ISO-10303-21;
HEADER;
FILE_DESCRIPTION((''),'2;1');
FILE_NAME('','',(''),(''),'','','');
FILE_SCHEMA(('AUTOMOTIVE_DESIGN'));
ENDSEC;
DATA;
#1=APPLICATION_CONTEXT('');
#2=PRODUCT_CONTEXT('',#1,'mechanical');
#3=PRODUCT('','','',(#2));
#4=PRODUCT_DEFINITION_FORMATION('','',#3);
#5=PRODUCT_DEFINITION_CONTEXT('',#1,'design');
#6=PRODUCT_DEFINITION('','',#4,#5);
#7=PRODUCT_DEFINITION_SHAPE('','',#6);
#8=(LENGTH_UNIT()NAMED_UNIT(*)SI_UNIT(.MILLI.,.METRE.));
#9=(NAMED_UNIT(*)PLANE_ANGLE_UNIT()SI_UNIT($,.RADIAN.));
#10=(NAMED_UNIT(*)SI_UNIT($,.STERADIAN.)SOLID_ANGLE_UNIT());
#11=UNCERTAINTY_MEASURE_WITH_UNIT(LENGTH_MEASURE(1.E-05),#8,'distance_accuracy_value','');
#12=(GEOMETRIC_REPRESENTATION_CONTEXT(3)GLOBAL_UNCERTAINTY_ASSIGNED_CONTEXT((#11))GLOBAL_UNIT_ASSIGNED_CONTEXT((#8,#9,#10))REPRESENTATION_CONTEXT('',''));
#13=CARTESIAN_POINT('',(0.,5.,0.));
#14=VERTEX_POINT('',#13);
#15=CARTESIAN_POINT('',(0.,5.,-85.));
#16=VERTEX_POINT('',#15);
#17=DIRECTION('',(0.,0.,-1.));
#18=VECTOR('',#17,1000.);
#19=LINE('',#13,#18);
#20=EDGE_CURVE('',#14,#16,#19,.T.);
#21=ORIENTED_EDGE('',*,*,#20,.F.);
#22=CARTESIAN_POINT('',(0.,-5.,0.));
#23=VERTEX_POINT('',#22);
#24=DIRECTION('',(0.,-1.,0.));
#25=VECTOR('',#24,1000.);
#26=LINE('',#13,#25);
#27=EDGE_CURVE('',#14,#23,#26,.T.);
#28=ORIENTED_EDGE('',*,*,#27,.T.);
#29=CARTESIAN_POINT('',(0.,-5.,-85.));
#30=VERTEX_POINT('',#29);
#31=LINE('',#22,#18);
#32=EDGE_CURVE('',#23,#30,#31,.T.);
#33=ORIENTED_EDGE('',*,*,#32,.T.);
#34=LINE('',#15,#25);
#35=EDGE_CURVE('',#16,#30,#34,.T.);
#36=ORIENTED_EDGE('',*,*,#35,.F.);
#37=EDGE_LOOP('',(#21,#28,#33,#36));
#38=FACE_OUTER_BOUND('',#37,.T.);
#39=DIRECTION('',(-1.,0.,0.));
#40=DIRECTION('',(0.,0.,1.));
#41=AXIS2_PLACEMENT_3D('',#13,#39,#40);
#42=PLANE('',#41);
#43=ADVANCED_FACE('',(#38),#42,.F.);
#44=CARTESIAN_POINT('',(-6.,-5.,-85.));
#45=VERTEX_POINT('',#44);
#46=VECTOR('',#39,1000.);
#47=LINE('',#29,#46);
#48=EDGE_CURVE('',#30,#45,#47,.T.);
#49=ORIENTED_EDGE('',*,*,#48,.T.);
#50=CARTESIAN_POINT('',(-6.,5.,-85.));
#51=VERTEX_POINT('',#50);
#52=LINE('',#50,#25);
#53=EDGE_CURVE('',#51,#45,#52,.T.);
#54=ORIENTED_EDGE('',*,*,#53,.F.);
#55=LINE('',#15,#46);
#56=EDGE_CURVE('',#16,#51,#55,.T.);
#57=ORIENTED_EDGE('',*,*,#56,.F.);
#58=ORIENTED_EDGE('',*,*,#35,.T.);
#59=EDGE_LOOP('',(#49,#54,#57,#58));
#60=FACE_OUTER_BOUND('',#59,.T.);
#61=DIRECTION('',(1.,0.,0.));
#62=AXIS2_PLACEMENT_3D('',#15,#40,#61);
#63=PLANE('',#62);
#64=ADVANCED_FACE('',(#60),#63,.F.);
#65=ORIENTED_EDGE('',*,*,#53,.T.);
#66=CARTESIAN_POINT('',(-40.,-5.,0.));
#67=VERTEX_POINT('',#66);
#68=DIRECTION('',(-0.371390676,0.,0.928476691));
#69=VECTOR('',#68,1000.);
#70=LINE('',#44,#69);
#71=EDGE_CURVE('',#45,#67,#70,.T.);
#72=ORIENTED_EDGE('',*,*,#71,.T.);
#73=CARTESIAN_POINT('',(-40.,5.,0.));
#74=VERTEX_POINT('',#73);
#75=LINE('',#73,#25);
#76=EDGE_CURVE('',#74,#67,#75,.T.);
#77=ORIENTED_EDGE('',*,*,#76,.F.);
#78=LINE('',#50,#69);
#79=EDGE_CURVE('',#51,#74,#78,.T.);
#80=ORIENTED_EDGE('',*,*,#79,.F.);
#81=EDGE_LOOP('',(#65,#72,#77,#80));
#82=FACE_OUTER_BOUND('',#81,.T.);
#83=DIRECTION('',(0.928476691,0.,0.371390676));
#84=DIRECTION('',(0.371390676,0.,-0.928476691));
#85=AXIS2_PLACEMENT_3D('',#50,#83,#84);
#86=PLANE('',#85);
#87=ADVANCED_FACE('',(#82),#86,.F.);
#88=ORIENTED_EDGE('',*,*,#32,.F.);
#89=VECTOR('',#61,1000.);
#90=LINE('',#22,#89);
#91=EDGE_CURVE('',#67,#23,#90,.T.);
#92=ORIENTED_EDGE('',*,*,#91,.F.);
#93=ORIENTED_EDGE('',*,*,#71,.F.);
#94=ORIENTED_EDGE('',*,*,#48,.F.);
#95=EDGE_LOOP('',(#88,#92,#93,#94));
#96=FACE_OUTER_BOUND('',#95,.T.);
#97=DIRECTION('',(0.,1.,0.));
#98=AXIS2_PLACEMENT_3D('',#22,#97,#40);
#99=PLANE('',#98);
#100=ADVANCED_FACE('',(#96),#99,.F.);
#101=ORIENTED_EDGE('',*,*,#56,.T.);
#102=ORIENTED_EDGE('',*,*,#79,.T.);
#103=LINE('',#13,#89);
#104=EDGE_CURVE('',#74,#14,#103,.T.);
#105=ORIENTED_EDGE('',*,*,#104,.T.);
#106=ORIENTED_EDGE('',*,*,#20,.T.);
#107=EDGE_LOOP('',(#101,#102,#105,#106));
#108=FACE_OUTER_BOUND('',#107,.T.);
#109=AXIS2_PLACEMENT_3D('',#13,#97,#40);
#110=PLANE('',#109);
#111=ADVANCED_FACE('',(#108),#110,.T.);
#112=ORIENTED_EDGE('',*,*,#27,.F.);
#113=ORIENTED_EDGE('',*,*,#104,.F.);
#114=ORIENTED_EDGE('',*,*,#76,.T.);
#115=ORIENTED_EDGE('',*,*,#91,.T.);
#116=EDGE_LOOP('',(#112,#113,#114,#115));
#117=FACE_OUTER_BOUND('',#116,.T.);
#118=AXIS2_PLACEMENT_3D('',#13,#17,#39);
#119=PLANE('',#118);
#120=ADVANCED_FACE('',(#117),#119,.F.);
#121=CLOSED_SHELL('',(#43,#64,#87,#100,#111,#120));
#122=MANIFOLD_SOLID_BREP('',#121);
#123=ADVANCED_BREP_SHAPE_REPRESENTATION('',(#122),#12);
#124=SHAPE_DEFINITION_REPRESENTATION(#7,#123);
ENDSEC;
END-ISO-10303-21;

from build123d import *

# Parameters (mm, degrees)
BOSS_EXTRUDE1_DEPTH = 5


with BuildPart() as part:
    # Sketch1 → Boss-Extrude1 (new, symmetric)
    with BuildSketch(Plane(origin=(0, 0, 0), x_dir=(1, 0, 0), z_dir=(0, 1, 0))):
        Polygon((-6, 85), (-40, 0), (0, 0), (0, 85), align=None)
    extrude(amount=BOSS_EXTRUDE1_DEPTH, both=True)


solid = part.part
